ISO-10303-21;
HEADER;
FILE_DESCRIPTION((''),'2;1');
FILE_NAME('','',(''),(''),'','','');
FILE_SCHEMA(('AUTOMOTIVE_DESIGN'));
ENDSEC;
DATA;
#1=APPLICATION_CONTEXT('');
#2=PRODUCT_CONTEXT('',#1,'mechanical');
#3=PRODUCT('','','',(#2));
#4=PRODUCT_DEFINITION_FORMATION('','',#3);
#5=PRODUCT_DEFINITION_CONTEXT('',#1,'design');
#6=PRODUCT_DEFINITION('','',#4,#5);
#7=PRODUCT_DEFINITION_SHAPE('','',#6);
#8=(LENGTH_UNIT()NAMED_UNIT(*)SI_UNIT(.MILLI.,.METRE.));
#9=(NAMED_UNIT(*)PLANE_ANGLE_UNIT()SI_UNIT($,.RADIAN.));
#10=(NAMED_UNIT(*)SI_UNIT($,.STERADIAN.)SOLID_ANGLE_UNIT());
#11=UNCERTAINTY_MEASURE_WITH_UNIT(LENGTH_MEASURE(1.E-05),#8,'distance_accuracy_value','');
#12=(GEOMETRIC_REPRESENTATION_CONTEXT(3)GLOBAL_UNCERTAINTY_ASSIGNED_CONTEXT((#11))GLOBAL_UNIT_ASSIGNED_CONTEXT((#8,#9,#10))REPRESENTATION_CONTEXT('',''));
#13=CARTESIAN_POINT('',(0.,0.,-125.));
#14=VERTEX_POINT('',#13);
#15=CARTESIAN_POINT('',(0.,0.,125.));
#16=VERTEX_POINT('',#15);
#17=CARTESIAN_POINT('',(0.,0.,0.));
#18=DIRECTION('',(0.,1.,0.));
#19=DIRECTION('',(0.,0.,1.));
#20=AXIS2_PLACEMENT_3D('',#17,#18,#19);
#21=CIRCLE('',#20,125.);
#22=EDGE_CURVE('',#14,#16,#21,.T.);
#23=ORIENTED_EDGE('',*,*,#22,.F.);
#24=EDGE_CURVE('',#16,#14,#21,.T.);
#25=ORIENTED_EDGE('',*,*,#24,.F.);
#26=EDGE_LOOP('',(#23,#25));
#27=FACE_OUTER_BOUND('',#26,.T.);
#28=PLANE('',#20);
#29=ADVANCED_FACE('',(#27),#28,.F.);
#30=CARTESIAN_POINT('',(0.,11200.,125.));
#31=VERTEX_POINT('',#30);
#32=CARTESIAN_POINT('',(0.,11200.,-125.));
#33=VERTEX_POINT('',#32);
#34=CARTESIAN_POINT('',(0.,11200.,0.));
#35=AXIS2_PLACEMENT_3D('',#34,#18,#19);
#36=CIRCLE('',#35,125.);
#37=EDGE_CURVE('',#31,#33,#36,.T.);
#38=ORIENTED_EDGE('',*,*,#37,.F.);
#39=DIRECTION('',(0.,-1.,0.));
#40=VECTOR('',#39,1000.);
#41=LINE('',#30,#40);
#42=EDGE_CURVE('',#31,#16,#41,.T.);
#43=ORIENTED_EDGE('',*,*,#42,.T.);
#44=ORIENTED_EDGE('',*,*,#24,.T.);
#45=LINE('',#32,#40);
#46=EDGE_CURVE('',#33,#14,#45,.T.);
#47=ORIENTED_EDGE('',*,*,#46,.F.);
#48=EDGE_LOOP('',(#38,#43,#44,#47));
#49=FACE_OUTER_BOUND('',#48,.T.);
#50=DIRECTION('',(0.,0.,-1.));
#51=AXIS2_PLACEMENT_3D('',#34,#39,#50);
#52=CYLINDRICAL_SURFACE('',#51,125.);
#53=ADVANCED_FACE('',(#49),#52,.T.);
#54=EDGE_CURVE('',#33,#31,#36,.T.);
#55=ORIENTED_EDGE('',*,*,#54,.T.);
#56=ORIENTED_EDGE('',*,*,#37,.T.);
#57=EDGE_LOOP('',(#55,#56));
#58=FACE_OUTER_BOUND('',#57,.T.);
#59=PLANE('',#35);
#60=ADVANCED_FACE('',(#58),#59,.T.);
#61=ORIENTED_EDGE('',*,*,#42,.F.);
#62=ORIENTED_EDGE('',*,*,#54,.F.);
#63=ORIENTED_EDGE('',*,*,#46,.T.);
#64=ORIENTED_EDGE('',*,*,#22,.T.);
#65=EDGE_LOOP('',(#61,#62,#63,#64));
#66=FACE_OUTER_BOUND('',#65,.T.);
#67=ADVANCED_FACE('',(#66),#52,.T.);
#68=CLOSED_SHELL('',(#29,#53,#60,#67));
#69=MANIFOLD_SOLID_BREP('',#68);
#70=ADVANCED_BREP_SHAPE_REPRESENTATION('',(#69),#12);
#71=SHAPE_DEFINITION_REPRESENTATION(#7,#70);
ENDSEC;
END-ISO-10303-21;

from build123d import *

# Parameters (mm, degrees)
SKETCH1_R           = 125
BOSS_EXTRUDE1_DEPTH = 11200


with BuildPart() as part:
    # Sketch1 → Boss-Extrude1 (new body)
    with BuildSketch(Plane(origin=(0, 0, 0), x_dir=(1, 0, 0), z_dir=(0, 1, 0))):
        with Locations(Location((0, 0, 0), (0, 0, 270))):
            Circle(SKETCH1_R)
    extrude(amount=BOSS_EXTRUDE1_DEPTH)


solid = part.part
